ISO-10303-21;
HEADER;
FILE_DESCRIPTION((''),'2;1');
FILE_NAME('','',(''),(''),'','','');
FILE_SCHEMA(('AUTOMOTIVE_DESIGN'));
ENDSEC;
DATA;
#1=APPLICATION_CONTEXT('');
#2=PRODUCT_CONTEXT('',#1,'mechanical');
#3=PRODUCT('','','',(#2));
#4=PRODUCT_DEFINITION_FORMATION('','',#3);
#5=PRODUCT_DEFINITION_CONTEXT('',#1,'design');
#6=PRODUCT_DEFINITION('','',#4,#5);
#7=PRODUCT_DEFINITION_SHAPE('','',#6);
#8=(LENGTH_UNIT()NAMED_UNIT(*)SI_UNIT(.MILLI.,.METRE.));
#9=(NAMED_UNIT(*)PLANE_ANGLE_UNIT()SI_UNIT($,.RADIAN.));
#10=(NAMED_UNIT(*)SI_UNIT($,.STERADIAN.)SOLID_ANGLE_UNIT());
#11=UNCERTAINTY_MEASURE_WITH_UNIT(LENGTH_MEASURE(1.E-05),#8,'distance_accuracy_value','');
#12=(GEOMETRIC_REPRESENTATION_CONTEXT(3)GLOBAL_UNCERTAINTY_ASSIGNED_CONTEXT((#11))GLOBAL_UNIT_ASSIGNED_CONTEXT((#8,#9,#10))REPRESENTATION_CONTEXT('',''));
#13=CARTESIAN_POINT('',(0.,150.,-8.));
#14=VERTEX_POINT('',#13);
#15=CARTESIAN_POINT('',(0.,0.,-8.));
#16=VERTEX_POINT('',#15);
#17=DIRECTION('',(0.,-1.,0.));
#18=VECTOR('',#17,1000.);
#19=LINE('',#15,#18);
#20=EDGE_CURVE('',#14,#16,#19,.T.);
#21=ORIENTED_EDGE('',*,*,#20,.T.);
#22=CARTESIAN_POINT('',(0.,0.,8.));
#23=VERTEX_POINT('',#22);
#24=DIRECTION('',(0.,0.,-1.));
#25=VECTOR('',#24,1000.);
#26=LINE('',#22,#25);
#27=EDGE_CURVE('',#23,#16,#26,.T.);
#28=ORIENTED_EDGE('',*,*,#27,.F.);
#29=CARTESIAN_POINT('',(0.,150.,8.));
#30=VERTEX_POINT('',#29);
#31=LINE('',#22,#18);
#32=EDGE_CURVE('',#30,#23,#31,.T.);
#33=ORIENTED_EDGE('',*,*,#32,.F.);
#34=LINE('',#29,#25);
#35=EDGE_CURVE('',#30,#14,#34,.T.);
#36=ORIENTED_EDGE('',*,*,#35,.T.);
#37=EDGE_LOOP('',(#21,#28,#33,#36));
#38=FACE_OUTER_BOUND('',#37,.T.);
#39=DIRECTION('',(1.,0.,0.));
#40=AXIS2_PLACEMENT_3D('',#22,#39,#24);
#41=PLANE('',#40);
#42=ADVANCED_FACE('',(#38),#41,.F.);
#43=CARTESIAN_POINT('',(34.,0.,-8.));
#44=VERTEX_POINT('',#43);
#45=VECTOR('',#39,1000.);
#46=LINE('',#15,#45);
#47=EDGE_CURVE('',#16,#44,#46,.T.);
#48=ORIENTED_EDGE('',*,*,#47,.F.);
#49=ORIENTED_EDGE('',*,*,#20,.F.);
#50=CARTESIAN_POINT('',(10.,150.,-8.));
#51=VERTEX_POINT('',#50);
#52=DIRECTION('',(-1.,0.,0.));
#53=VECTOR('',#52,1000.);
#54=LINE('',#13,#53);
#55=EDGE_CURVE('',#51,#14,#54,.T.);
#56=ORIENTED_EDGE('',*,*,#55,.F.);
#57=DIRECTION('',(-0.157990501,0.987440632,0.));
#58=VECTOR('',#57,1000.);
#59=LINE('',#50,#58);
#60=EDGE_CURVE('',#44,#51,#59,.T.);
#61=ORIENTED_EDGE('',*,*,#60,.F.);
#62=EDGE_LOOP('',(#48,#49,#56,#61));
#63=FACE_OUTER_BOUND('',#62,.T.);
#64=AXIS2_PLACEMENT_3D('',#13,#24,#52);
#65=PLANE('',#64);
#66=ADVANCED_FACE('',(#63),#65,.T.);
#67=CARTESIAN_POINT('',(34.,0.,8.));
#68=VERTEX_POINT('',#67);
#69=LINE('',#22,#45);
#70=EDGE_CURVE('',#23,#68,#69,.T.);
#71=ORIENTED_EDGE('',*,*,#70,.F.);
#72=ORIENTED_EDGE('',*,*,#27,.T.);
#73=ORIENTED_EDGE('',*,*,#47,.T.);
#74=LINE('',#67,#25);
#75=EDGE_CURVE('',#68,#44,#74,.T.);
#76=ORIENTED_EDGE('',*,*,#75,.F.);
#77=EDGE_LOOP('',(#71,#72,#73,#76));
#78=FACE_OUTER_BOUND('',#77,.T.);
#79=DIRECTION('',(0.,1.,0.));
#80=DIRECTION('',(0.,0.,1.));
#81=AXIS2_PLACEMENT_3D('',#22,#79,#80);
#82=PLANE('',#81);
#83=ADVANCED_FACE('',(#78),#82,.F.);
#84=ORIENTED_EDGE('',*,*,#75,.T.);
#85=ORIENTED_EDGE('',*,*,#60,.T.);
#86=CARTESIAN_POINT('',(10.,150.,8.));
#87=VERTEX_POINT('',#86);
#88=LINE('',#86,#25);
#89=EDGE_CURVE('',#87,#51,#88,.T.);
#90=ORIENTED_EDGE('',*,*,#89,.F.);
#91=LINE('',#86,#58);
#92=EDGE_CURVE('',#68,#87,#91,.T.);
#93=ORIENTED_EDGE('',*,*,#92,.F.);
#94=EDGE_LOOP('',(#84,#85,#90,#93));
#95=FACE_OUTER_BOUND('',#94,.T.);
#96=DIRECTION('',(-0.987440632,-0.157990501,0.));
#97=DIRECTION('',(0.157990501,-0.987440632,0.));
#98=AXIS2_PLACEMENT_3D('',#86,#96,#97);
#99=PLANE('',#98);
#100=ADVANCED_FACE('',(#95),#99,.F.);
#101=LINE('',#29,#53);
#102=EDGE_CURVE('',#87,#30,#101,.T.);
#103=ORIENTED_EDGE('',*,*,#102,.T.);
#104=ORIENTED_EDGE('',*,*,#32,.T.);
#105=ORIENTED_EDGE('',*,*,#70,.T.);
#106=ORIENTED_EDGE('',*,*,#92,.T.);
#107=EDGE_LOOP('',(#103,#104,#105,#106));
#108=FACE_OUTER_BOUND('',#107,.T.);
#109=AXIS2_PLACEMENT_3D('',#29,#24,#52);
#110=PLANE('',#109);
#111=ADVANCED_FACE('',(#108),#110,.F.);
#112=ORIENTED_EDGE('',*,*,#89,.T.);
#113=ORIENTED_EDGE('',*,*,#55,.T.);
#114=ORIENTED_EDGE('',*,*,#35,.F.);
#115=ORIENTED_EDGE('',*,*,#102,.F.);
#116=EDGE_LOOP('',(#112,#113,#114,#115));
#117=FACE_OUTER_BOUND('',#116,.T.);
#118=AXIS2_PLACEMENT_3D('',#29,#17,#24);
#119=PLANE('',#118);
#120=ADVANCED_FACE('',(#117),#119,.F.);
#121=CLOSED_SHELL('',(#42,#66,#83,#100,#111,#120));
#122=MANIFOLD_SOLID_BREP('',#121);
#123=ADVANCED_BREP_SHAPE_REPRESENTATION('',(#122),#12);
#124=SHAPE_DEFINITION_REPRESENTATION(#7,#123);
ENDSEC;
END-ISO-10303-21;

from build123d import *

# Parameters (mm, degrees)
EXTRUDE1_DEPTH = 8


with BuildPart() as part:
    # Sketch1 → Extrude1 (new, symmetric)
    with BuildSketch(Plane.XY):
        Polygon((0, 0), (34, 0), (10, 150), (0, 150), align=None)
    extrude(amount=EXTRUDE1_DEPTH, both=True)


solid = part.part
